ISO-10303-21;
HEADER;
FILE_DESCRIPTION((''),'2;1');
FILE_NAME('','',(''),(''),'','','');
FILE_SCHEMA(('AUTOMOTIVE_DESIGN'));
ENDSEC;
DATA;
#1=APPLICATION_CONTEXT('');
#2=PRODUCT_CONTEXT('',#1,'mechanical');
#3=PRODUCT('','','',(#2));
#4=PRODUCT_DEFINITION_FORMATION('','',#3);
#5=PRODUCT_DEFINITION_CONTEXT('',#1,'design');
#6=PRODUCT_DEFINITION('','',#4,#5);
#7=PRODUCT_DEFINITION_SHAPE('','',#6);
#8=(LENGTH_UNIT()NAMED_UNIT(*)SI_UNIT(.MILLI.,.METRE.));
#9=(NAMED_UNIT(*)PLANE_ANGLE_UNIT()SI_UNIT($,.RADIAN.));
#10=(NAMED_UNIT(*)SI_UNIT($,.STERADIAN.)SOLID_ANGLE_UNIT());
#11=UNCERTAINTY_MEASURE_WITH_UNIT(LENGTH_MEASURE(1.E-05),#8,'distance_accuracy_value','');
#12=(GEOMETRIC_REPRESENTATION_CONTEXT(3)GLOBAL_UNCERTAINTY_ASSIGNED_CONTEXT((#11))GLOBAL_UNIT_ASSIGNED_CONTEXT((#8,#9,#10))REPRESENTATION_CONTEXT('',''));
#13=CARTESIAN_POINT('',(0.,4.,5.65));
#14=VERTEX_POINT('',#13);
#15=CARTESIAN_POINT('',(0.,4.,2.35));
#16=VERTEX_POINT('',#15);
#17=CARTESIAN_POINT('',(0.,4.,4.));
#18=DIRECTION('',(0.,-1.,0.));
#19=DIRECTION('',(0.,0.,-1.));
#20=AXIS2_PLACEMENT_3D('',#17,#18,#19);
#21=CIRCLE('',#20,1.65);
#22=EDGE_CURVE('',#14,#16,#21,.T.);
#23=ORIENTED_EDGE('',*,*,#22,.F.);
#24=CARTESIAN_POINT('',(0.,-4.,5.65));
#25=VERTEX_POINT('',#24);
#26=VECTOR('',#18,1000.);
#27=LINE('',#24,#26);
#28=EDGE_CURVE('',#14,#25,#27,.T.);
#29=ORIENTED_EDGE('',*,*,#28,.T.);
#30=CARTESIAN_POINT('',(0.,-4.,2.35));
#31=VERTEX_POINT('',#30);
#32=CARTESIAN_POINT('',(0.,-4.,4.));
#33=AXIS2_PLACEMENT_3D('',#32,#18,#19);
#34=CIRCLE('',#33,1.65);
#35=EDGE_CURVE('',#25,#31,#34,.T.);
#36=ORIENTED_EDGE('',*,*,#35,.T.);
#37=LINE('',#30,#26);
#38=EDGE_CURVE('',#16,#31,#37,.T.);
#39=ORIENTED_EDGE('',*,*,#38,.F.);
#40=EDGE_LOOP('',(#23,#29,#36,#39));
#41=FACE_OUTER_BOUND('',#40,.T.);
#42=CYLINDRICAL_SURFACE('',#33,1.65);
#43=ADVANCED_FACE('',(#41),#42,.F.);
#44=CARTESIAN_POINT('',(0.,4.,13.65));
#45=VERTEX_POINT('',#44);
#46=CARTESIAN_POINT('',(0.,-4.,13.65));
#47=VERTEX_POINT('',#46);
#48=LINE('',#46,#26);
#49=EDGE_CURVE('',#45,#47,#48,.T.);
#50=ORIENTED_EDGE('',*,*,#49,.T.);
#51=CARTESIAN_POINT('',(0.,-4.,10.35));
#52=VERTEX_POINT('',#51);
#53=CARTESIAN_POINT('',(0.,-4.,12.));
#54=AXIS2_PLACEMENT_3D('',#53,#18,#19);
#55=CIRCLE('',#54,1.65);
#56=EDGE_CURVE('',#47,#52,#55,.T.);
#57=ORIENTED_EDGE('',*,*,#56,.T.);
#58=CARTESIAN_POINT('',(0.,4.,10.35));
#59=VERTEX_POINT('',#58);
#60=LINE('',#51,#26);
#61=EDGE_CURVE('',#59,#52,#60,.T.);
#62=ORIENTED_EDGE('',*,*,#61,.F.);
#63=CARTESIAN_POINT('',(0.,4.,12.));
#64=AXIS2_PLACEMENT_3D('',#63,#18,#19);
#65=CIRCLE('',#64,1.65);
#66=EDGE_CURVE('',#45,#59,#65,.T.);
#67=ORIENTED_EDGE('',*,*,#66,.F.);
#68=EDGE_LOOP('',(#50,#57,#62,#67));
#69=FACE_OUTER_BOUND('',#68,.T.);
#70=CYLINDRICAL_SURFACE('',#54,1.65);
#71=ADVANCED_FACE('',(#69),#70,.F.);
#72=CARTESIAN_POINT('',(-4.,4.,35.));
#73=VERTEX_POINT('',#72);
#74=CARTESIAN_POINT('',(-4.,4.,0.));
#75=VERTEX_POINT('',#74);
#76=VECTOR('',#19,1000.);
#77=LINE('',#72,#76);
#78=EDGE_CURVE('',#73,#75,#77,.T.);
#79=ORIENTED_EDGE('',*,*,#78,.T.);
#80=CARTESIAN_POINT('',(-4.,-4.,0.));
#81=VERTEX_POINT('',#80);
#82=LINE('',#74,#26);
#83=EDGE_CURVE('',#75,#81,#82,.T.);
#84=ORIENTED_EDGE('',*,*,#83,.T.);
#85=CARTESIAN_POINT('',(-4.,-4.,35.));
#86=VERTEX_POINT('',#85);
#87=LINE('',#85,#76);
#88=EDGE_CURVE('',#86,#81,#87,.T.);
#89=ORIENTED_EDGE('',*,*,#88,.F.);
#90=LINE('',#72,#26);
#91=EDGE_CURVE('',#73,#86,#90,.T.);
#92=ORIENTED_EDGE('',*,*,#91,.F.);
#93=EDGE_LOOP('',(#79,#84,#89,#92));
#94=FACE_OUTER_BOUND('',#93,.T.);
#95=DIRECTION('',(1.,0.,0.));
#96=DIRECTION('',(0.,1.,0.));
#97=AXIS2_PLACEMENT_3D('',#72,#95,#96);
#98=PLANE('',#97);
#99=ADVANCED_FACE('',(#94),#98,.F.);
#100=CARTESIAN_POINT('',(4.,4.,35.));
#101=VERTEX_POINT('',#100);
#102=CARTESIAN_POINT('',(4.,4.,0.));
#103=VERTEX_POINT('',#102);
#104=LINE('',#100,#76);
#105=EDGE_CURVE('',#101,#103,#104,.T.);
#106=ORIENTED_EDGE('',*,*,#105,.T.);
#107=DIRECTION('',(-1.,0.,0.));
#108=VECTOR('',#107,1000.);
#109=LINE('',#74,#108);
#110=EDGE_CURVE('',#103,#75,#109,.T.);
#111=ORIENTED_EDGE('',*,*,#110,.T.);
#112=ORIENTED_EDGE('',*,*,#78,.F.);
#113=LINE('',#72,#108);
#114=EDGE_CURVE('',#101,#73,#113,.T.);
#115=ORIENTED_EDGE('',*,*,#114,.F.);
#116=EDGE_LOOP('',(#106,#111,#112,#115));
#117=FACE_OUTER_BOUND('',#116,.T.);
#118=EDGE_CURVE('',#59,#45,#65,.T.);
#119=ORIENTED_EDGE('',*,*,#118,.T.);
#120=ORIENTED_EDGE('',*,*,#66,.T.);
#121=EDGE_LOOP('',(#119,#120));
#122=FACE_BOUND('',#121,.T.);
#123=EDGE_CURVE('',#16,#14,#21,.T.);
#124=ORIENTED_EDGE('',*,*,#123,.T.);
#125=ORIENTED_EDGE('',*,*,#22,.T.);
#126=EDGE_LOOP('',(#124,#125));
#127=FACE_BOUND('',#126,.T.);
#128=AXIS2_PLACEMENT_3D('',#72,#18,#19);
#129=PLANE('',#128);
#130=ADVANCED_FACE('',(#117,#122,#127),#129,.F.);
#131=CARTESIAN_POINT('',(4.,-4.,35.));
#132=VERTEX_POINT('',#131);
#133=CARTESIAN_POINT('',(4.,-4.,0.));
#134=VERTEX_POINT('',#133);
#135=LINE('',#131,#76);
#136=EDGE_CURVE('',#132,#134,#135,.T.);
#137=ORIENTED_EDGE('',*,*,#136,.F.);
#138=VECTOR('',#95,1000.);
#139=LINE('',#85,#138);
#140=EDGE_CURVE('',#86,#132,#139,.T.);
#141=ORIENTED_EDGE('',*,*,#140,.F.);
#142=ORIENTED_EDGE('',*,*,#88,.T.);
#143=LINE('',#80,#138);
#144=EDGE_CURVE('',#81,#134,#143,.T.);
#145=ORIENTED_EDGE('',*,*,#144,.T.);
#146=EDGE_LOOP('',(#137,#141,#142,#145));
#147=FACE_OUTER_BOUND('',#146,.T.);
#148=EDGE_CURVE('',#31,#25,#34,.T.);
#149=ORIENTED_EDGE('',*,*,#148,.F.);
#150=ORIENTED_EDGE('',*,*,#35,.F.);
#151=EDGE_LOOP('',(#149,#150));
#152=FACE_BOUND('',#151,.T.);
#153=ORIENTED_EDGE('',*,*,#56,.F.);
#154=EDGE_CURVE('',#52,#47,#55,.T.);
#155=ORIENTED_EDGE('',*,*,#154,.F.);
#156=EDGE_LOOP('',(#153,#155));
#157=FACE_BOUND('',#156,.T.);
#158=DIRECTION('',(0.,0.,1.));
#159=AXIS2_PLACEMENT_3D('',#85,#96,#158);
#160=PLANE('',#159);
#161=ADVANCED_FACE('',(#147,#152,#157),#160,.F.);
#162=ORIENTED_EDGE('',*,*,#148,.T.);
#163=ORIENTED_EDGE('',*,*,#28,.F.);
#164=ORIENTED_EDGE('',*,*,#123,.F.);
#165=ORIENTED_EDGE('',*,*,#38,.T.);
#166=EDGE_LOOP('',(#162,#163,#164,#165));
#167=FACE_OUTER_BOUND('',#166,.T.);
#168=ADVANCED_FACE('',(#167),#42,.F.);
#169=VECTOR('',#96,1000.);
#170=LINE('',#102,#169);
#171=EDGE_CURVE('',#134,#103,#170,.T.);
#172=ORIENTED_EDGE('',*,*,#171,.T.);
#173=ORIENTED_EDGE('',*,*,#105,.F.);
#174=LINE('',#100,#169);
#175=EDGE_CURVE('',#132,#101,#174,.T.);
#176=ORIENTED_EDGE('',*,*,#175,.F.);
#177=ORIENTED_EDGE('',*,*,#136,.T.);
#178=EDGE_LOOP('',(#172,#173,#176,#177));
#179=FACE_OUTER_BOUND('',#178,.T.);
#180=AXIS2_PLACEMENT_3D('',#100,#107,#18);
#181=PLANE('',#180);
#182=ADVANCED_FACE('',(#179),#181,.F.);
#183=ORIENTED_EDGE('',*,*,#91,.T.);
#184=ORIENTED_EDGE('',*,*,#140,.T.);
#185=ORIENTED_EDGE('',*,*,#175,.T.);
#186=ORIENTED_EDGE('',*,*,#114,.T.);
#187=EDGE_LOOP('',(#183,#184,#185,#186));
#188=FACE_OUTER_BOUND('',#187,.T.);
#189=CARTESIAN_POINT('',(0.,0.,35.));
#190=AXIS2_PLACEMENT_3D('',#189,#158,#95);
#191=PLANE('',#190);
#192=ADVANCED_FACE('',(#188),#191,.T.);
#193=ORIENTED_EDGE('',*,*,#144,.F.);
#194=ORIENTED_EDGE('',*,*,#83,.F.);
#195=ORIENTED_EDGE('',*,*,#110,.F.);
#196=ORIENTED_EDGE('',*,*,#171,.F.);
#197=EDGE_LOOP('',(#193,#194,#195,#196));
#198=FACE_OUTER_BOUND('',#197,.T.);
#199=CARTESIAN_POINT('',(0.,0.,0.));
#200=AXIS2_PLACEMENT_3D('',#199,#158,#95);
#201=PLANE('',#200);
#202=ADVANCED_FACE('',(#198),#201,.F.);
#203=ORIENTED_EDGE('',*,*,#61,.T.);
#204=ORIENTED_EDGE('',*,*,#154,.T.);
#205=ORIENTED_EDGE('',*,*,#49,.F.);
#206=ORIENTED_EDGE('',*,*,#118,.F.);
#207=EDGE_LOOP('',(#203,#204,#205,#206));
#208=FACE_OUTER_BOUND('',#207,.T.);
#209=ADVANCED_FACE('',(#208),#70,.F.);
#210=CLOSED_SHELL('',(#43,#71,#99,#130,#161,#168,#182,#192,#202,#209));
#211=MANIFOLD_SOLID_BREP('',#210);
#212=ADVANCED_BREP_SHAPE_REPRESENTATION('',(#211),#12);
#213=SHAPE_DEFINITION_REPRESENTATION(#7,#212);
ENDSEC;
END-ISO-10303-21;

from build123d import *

# Parameters (mm, degrees)
SKETCH_1_W         = 8
SKETCH_1_H         = 8
EXTRUDE_1_DEPTH    = 35
HOLE_WIZARD_M4_1_D = 3.3


with BuildPart() as part:
    # 草图1 → 凸台-拉伸1 (new body)
    with BuildSketch(Plane.XY):
        Rectangle(SKETCH_1_W, SKETCH_1_H)
    extrude(amount=EXTRUDE_1_DEPTH)

    # M4 螺纹孔1 (through all)
    with Locations(Plane(origin=(0, -4, 0), x_dir=(-1, 0, 0), z_dir=(0, -1, 0))):
        with Locations((0, -12), (0, -4)):
            Hole(HOLE_WIZARD_M4_1_D / 2)


solid = part.part
